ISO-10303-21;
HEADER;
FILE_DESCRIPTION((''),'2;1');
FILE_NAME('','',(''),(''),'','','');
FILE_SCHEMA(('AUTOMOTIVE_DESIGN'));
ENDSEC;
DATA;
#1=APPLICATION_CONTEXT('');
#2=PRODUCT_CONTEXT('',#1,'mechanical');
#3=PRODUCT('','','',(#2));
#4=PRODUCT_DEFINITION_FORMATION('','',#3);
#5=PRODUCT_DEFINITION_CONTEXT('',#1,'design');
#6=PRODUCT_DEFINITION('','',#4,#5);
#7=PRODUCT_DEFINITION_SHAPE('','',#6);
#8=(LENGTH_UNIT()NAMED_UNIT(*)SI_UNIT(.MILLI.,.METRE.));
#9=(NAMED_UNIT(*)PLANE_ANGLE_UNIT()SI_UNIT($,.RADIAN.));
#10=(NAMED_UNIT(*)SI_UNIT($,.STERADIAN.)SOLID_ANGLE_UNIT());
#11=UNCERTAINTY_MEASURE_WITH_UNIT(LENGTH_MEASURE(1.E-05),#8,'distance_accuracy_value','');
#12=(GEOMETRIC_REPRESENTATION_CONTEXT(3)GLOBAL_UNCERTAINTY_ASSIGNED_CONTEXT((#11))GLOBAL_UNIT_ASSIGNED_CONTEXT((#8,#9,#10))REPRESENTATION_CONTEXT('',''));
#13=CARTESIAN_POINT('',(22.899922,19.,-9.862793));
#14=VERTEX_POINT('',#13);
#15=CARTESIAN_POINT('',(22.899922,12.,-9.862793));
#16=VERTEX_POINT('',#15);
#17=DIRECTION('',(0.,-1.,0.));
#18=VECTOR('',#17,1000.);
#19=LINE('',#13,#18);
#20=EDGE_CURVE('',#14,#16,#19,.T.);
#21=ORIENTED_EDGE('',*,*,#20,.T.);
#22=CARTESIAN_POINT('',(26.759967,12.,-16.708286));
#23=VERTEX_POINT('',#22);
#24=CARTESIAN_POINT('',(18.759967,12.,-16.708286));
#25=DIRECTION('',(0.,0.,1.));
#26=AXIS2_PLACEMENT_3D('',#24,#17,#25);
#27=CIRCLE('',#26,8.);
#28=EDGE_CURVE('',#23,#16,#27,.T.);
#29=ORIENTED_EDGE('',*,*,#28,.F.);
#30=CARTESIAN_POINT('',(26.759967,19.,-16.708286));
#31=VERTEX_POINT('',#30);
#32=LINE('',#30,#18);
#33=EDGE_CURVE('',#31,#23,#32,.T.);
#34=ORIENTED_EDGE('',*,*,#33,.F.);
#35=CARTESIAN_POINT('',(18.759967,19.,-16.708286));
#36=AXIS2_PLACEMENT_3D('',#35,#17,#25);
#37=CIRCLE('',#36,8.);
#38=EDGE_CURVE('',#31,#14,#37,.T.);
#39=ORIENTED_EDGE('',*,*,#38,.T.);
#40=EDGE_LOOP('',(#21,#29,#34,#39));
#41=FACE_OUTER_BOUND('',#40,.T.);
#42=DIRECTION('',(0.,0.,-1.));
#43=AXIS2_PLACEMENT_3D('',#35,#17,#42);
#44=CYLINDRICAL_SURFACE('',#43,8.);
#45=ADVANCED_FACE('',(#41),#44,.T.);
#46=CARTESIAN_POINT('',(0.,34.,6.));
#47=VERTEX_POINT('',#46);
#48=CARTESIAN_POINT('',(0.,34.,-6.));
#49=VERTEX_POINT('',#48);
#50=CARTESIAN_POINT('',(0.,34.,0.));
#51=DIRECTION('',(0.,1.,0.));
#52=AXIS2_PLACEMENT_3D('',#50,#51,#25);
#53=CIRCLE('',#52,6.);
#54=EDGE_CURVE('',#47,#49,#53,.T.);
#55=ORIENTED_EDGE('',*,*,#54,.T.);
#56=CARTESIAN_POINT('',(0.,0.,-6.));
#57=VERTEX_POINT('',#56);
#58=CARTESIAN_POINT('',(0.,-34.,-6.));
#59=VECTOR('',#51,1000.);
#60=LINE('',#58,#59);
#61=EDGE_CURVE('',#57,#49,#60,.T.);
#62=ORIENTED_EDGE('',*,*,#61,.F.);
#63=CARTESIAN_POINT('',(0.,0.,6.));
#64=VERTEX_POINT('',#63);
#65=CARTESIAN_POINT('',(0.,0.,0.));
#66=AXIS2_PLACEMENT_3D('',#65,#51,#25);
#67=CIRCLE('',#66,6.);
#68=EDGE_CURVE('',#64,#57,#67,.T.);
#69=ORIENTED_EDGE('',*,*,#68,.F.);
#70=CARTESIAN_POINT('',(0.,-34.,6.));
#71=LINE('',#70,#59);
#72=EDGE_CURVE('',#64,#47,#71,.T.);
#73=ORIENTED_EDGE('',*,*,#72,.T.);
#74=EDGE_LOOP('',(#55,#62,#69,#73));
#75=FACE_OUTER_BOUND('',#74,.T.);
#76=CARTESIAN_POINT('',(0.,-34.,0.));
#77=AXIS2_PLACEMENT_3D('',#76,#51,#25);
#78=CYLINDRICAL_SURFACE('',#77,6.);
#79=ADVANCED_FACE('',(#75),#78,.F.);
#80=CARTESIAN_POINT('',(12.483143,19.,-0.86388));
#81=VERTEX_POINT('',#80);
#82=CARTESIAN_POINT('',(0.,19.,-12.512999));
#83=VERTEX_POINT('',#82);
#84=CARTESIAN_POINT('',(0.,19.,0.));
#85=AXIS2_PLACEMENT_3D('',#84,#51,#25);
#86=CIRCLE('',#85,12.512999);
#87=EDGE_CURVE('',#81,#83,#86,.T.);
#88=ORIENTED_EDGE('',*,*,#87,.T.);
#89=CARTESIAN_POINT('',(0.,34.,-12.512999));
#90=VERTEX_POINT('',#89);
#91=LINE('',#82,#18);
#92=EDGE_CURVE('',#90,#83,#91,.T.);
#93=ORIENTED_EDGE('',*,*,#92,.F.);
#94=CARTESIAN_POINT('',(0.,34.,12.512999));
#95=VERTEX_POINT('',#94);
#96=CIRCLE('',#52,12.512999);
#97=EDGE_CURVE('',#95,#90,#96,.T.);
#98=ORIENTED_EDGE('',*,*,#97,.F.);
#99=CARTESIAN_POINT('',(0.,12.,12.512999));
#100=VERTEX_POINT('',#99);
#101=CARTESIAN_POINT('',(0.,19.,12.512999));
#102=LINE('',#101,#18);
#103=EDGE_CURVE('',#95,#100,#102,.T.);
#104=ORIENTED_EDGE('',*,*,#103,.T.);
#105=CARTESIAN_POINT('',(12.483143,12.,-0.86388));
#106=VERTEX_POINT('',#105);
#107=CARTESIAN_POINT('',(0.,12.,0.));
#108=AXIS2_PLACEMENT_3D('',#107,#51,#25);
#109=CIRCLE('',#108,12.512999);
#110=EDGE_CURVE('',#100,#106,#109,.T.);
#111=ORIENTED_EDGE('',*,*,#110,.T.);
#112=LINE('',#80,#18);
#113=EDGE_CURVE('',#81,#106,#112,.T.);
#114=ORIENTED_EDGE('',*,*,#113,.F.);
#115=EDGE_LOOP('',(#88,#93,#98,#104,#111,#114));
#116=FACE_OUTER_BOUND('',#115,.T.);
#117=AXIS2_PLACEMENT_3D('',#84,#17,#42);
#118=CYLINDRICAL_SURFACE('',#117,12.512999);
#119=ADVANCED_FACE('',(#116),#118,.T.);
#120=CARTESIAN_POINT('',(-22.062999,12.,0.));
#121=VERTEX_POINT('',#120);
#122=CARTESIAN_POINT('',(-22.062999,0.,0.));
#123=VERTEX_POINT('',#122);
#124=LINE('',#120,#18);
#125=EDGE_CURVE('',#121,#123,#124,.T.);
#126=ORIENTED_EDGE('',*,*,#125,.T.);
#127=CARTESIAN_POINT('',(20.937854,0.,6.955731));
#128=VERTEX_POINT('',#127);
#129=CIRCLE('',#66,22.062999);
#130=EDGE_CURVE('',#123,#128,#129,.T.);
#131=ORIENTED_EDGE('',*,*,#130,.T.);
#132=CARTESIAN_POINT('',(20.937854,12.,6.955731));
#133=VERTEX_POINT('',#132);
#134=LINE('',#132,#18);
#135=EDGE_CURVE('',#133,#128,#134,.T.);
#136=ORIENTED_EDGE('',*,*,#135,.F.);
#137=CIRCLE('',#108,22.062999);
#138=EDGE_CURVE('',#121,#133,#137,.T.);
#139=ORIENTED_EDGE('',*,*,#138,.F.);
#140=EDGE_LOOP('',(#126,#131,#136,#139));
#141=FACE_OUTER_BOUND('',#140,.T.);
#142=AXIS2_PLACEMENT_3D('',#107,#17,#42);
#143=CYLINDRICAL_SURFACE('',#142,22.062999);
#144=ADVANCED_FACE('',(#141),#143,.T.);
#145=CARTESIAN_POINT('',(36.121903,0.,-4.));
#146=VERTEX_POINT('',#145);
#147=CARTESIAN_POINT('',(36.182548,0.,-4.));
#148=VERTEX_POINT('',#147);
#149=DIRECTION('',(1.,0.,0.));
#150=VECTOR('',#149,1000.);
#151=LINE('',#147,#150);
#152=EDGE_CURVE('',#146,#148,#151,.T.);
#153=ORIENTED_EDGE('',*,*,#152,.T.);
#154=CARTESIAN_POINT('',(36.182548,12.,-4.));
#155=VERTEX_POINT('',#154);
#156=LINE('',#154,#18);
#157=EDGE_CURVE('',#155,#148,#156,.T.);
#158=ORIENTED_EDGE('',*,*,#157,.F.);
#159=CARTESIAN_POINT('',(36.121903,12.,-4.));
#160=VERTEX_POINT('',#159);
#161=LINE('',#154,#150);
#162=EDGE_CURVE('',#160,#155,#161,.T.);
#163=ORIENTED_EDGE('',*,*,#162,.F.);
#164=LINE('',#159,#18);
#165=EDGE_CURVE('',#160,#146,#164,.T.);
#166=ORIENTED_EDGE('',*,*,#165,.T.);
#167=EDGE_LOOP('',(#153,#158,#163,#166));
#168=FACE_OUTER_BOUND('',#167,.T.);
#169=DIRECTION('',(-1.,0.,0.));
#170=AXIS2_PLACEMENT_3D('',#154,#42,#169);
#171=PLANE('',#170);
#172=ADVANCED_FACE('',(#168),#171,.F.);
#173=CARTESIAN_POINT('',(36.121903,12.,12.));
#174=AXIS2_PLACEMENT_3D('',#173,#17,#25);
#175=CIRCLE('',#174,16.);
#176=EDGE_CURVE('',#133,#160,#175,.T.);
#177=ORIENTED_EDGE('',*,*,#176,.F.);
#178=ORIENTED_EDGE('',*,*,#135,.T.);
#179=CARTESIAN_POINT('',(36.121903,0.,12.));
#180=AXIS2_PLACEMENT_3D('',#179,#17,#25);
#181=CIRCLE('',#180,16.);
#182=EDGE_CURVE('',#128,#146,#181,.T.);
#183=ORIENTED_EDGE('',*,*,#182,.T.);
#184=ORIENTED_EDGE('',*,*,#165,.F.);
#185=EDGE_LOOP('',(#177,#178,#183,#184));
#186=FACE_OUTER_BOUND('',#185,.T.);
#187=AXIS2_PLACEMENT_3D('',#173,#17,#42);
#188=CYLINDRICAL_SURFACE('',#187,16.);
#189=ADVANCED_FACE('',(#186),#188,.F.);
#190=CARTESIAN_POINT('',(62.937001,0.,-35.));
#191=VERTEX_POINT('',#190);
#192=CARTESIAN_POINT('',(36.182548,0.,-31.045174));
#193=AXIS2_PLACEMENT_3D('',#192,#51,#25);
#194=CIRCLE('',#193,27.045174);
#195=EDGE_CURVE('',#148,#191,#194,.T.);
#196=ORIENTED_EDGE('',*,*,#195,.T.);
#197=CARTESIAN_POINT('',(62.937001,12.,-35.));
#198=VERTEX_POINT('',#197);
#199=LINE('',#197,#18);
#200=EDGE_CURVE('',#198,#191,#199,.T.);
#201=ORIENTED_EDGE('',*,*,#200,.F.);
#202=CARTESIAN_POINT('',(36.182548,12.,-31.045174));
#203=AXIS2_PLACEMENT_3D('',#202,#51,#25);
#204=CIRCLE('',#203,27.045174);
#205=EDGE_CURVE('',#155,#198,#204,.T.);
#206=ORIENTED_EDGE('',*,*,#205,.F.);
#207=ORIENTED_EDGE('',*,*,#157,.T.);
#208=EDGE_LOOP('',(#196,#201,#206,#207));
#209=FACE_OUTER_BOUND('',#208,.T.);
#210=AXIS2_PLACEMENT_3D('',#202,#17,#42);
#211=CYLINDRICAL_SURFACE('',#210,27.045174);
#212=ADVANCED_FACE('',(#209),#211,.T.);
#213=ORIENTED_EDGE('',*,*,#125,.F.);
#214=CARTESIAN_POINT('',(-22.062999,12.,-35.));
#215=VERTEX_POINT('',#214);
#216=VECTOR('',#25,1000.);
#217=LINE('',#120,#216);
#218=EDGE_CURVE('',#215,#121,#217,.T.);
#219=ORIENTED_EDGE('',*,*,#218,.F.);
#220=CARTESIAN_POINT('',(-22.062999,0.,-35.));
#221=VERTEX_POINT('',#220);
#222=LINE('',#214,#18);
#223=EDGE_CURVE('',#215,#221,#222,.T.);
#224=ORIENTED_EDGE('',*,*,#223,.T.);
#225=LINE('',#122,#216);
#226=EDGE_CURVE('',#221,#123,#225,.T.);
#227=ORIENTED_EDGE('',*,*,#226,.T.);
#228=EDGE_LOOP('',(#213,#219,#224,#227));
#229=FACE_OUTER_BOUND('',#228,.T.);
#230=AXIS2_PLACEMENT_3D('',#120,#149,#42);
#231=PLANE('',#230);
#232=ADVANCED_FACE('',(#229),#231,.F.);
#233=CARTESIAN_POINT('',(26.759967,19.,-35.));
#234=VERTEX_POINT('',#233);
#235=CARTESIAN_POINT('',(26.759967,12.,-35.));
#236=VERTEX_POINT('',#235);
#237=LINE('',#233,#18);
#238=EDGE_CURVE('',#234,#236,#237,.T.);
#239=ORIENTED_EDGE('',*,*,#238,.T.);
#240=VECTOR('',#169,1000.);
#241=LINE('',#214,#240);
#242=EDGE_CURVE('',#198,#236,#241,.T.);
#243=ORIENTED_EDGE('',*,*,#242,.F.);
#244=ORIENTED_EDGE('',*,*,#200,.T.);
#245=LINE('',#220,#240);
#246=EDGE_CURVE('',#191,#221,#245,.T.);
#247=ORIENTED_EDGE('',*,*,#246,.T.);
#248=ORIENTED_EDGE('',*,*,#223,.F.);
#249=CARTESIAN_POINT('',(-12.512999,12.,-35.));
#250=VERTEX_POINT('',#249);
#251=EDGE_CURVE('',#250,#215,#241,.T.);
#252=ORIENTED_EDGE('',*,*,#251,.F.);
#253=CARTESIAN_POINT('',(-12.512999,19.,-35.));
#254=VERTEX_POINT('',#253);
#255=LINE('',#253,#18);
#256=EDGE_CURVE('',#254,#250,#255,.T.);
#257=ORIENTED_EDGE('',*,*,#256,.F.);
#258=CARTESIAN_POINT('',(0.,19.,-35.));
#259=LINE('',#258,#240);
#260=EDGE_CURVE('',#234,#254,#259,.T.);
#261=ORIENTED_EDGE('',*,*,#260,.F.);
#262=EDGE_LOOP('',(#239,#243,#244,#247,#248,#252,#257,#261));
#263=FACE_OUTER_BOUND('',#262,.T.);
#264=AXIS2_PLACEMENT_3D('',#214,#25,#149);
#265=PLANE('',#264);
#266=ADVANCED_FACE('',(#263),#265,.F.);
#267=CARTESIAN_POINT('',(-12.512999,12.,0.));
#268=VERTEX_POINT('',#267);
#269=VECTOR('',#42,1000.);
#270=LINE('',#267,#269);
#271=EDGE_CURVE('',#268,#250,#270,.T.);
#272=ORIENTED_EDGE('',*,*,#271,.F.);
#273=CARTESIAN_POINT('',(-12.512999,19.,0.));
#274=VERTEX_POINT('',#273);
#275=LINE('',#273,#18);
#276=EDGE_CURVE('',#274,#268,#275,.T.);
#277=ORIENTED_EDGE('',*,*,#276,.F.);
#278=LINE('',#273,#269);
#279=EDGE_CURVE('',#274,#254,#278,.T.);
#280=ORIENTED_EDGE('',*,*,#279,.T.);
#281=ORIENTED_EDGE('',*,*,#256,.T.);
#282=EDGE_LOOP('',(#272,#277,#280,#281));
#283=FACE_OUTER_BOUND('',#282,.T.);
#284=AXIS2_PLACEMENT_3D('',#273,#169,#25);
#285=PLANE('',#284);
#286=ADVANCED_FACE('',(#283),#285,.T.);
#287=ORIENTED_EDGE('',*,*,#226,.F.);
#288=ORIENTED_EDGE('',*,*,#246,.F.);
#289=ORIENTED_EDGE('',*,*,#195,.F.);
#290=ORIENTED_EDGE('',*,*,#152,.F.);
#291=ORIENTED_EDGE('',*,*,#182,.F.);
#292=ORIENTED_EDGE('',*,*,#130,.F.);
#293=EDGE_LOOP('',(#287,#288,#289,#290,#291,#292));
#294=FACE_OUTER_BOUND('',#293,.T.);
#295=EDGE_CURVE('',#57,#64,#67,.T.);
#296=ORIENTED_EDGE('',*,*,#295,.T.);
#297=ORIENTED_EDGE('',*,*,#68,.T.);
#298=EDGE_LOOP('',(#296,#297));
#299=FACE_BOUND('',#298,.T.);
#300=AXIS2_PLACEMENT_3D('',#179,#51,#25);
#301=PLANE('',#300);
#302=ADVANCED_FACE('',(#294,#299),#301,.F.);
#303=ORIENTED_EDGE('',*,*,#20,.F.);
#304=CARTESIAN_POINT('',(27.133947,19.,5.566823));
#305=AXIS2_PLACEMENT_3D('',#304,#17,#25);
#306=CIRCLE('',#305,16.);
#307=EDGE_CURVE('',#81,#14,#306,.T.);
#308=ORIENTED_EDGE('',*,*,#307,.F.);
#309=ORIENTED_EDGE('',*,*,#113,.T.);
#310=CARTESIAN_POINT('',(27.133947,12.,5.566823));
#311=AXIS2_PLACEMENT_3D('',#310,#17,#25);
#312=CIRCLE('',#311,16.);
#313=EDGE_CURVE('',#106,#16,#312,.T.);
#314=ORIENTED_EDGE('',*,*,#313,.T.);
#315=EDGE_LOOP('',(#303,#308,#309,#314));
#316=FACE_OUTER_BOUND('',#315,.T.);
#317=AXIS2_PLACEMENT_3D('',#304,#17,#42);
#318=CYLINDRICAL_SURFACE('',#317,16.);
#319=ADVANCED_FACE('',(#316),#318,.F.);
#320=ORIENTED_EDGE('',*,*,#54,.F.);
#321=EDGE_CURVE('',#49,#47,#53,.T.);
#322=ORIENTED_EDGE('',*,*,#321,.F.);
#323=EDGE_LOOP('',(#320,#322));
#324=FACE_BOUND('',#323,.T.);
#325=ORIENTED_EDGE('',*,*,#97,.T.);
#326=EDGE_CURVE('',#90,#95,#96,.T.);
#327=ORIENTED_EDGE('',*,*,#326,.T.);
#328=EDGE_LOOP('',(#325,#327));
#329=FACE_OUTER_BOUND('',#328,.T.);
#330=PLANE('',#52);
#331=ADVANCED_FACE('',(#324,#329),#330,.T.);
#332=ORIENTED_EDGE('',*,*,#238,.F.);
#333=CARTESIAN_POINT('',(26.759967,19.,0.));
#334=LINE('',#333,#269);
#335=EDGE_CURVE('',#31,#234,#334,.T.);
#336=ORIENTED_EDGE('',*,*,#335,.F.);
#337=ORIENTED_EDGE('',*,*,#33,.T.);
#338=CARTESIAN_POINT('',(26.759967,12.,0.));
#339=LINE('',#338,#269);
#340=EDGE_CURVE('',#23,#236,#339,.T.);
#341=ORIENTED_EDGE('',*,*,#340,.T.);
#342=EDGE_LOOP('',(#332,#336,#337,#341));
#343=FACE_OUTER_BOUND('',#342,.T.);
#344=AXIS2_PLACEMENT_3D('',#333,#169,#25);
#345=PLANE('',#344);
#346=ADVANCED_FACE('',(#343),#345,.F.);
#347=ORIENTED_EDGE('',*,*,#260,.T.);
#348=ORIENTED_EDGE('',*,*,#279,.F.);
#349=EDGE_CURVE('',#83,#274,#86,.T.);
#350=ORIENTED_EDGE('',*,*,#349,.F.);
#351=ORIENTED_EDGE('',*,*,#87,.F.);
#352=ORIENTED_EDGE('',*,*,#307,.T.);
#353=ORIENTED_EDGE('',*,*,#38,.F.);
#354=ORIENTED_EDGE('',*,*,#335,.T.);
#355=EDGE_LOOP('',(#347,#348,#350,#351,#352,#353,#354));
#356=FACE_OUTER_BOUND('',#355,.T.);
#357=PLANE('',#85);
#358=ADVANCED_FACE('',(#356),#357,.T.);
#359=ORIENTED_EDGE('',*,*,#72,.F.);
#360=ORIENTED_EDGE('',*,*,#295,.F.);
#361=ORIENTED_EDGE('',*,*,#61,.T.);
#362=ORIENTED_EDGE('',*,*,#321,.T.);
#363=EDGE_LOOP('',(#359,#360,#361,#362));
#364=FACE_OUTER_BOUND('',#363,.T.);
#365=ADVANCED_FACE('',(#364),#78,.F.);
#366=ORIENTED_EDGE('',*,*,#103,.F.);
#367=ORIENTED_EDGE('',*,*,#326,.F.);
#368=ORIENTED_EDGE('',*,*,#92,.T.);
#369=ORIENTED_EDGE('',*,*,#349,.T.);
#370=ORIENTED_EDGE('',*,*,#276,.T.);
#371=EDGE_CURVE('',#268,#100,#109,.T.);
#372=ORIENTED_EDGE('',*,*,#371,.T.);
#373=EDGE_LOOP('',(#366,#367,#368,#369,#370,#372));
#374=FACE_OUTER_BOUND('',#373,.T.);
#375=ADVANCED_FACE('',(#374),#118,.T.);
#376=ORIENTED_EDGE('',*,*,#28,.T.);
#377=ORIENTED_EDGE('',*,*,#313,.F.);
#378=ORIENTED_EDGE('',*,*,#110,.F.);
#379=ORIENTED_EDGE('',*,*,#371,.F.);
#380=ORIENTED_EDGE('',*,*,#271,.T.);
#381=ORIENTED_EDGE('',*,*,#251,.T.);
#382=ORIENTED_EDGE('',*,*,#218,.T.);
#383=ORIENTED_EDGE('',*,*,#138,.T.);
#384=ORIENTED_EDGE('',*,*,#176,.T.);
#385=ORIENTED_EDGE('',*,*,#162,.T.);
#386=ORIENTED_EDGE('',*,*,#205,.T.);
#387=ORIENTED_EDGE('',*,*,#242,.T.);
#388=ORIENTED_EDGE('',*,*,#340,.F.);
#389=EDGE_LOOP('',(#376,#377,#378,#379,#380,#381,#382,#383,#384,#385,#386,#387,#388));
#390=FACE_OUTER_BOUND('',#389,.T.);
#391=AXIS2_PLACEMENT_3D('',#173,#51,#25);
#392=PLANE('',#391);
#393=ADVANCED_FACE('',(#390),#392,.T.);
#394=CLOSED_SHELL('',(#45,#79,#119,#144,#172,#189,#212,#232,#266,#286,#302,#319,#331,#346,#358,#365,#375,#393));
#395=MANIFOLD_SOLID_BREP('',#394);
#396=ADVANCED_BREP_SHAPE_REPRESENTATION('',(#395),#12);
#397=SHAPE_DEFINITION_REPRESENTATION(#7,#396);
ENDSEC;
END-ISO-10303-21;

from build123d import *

# Parameters (mm, degrees)
BASE_PLATE_DEPTH   = 12
RAISED_PAD_DEPTH   = 7
HUB_BOSS_PROFILE_R = 12.512998998
HUB_BOSS_DEPTH     = 15
BORE_12_PROFILE_R  = 6
BORE_12_DEPTH      = 68


with BuildPart() as part:
    # Base Plate Profile → Base Plate (new body)
    with BuildSketch(Plane(origin=(0, 0, 0), x_dir=(1, 0, 0), z_dir=(0, 1, 0))):
        with BuildLine():
            Line((-22.062998998, 0), (-22.062998998, 35))
            Line((-22.062998998, 35), (62.937001002, 35))
            ThreePointArc((62.937001002, 35), (56.656926651, 13.374824859), (36.182547719, 4))
            Line((36.182547719, 4), (36.121903227, 4))
            ThreePointArc((36.121903227, 4), (26.759967036, 0.975135867), (20.93785397, -6.955731155))
            ThreePointArc((20.93785397, -6.955731155), (-3.52307207, -21.779896418), (-22.062998998, 0))
        make_face()
    extrude(amount=BASE_PLATE_DEPTH)

    # Raised Pad Profile → Raised Pad (add)
    with BuildSketch(Plane(origin=(0, 12, 0), x_dir=(1, 0, 0), z_dir=(0, 1, 0))):
        with BuildLine():
            Line((-12.512998998, 35), (-12.512998998, 0))
            ThreePointArc((-12.512998998, 0), (0.432197973, -12.505532729), (12.483142832, 0.863880178))
            ThreePointArc((12.483142832, 0.863880178), (16.674295928, 6.54084856), (22.899922014, 9.862792887))
            ThreePointArc((22.899922014, 9.862792887), (25.728454671, 12.778886311), (26.759967036, 16.708285768))
            Line((26.759967036, 16.708285768), (26.759967036, 35))
            Line((26.759967036, 35), (-12.512998998, 35))
        make_face()
    extrude(amount=RAISED_PAD_DEPTH)

    # Hub Boss Profile → Hub Boss (add)
    with BuildSketch(Plane(origin=(0, 19, 0), x_dir=(1, 0, 0), z_dir=(0, 1, 0))):
        with Locations(Location((0, 0, 0), (0, 0, 3.958770586))):
            Circle(HUB_BOSS_PROFILE_R)
    extrude(amount=HUB_BOSS_DEPTH)

    # Bore Ø12 Profile → Bore Ø12 (cut)
    with BuildSketch(Plane(origin=(0, 34, 0), x_dir=(1, 0, 0), z_dir=(0, 1, 0))):
        with Locations(Location((0, 0, 0), (0, 0, 270))):
            Circle(BORE_12_PROFILE_R)
    extrude(amount=-BORE_12_DEPTH, mode=Mode.SUBTRACT)


solid = part.part
